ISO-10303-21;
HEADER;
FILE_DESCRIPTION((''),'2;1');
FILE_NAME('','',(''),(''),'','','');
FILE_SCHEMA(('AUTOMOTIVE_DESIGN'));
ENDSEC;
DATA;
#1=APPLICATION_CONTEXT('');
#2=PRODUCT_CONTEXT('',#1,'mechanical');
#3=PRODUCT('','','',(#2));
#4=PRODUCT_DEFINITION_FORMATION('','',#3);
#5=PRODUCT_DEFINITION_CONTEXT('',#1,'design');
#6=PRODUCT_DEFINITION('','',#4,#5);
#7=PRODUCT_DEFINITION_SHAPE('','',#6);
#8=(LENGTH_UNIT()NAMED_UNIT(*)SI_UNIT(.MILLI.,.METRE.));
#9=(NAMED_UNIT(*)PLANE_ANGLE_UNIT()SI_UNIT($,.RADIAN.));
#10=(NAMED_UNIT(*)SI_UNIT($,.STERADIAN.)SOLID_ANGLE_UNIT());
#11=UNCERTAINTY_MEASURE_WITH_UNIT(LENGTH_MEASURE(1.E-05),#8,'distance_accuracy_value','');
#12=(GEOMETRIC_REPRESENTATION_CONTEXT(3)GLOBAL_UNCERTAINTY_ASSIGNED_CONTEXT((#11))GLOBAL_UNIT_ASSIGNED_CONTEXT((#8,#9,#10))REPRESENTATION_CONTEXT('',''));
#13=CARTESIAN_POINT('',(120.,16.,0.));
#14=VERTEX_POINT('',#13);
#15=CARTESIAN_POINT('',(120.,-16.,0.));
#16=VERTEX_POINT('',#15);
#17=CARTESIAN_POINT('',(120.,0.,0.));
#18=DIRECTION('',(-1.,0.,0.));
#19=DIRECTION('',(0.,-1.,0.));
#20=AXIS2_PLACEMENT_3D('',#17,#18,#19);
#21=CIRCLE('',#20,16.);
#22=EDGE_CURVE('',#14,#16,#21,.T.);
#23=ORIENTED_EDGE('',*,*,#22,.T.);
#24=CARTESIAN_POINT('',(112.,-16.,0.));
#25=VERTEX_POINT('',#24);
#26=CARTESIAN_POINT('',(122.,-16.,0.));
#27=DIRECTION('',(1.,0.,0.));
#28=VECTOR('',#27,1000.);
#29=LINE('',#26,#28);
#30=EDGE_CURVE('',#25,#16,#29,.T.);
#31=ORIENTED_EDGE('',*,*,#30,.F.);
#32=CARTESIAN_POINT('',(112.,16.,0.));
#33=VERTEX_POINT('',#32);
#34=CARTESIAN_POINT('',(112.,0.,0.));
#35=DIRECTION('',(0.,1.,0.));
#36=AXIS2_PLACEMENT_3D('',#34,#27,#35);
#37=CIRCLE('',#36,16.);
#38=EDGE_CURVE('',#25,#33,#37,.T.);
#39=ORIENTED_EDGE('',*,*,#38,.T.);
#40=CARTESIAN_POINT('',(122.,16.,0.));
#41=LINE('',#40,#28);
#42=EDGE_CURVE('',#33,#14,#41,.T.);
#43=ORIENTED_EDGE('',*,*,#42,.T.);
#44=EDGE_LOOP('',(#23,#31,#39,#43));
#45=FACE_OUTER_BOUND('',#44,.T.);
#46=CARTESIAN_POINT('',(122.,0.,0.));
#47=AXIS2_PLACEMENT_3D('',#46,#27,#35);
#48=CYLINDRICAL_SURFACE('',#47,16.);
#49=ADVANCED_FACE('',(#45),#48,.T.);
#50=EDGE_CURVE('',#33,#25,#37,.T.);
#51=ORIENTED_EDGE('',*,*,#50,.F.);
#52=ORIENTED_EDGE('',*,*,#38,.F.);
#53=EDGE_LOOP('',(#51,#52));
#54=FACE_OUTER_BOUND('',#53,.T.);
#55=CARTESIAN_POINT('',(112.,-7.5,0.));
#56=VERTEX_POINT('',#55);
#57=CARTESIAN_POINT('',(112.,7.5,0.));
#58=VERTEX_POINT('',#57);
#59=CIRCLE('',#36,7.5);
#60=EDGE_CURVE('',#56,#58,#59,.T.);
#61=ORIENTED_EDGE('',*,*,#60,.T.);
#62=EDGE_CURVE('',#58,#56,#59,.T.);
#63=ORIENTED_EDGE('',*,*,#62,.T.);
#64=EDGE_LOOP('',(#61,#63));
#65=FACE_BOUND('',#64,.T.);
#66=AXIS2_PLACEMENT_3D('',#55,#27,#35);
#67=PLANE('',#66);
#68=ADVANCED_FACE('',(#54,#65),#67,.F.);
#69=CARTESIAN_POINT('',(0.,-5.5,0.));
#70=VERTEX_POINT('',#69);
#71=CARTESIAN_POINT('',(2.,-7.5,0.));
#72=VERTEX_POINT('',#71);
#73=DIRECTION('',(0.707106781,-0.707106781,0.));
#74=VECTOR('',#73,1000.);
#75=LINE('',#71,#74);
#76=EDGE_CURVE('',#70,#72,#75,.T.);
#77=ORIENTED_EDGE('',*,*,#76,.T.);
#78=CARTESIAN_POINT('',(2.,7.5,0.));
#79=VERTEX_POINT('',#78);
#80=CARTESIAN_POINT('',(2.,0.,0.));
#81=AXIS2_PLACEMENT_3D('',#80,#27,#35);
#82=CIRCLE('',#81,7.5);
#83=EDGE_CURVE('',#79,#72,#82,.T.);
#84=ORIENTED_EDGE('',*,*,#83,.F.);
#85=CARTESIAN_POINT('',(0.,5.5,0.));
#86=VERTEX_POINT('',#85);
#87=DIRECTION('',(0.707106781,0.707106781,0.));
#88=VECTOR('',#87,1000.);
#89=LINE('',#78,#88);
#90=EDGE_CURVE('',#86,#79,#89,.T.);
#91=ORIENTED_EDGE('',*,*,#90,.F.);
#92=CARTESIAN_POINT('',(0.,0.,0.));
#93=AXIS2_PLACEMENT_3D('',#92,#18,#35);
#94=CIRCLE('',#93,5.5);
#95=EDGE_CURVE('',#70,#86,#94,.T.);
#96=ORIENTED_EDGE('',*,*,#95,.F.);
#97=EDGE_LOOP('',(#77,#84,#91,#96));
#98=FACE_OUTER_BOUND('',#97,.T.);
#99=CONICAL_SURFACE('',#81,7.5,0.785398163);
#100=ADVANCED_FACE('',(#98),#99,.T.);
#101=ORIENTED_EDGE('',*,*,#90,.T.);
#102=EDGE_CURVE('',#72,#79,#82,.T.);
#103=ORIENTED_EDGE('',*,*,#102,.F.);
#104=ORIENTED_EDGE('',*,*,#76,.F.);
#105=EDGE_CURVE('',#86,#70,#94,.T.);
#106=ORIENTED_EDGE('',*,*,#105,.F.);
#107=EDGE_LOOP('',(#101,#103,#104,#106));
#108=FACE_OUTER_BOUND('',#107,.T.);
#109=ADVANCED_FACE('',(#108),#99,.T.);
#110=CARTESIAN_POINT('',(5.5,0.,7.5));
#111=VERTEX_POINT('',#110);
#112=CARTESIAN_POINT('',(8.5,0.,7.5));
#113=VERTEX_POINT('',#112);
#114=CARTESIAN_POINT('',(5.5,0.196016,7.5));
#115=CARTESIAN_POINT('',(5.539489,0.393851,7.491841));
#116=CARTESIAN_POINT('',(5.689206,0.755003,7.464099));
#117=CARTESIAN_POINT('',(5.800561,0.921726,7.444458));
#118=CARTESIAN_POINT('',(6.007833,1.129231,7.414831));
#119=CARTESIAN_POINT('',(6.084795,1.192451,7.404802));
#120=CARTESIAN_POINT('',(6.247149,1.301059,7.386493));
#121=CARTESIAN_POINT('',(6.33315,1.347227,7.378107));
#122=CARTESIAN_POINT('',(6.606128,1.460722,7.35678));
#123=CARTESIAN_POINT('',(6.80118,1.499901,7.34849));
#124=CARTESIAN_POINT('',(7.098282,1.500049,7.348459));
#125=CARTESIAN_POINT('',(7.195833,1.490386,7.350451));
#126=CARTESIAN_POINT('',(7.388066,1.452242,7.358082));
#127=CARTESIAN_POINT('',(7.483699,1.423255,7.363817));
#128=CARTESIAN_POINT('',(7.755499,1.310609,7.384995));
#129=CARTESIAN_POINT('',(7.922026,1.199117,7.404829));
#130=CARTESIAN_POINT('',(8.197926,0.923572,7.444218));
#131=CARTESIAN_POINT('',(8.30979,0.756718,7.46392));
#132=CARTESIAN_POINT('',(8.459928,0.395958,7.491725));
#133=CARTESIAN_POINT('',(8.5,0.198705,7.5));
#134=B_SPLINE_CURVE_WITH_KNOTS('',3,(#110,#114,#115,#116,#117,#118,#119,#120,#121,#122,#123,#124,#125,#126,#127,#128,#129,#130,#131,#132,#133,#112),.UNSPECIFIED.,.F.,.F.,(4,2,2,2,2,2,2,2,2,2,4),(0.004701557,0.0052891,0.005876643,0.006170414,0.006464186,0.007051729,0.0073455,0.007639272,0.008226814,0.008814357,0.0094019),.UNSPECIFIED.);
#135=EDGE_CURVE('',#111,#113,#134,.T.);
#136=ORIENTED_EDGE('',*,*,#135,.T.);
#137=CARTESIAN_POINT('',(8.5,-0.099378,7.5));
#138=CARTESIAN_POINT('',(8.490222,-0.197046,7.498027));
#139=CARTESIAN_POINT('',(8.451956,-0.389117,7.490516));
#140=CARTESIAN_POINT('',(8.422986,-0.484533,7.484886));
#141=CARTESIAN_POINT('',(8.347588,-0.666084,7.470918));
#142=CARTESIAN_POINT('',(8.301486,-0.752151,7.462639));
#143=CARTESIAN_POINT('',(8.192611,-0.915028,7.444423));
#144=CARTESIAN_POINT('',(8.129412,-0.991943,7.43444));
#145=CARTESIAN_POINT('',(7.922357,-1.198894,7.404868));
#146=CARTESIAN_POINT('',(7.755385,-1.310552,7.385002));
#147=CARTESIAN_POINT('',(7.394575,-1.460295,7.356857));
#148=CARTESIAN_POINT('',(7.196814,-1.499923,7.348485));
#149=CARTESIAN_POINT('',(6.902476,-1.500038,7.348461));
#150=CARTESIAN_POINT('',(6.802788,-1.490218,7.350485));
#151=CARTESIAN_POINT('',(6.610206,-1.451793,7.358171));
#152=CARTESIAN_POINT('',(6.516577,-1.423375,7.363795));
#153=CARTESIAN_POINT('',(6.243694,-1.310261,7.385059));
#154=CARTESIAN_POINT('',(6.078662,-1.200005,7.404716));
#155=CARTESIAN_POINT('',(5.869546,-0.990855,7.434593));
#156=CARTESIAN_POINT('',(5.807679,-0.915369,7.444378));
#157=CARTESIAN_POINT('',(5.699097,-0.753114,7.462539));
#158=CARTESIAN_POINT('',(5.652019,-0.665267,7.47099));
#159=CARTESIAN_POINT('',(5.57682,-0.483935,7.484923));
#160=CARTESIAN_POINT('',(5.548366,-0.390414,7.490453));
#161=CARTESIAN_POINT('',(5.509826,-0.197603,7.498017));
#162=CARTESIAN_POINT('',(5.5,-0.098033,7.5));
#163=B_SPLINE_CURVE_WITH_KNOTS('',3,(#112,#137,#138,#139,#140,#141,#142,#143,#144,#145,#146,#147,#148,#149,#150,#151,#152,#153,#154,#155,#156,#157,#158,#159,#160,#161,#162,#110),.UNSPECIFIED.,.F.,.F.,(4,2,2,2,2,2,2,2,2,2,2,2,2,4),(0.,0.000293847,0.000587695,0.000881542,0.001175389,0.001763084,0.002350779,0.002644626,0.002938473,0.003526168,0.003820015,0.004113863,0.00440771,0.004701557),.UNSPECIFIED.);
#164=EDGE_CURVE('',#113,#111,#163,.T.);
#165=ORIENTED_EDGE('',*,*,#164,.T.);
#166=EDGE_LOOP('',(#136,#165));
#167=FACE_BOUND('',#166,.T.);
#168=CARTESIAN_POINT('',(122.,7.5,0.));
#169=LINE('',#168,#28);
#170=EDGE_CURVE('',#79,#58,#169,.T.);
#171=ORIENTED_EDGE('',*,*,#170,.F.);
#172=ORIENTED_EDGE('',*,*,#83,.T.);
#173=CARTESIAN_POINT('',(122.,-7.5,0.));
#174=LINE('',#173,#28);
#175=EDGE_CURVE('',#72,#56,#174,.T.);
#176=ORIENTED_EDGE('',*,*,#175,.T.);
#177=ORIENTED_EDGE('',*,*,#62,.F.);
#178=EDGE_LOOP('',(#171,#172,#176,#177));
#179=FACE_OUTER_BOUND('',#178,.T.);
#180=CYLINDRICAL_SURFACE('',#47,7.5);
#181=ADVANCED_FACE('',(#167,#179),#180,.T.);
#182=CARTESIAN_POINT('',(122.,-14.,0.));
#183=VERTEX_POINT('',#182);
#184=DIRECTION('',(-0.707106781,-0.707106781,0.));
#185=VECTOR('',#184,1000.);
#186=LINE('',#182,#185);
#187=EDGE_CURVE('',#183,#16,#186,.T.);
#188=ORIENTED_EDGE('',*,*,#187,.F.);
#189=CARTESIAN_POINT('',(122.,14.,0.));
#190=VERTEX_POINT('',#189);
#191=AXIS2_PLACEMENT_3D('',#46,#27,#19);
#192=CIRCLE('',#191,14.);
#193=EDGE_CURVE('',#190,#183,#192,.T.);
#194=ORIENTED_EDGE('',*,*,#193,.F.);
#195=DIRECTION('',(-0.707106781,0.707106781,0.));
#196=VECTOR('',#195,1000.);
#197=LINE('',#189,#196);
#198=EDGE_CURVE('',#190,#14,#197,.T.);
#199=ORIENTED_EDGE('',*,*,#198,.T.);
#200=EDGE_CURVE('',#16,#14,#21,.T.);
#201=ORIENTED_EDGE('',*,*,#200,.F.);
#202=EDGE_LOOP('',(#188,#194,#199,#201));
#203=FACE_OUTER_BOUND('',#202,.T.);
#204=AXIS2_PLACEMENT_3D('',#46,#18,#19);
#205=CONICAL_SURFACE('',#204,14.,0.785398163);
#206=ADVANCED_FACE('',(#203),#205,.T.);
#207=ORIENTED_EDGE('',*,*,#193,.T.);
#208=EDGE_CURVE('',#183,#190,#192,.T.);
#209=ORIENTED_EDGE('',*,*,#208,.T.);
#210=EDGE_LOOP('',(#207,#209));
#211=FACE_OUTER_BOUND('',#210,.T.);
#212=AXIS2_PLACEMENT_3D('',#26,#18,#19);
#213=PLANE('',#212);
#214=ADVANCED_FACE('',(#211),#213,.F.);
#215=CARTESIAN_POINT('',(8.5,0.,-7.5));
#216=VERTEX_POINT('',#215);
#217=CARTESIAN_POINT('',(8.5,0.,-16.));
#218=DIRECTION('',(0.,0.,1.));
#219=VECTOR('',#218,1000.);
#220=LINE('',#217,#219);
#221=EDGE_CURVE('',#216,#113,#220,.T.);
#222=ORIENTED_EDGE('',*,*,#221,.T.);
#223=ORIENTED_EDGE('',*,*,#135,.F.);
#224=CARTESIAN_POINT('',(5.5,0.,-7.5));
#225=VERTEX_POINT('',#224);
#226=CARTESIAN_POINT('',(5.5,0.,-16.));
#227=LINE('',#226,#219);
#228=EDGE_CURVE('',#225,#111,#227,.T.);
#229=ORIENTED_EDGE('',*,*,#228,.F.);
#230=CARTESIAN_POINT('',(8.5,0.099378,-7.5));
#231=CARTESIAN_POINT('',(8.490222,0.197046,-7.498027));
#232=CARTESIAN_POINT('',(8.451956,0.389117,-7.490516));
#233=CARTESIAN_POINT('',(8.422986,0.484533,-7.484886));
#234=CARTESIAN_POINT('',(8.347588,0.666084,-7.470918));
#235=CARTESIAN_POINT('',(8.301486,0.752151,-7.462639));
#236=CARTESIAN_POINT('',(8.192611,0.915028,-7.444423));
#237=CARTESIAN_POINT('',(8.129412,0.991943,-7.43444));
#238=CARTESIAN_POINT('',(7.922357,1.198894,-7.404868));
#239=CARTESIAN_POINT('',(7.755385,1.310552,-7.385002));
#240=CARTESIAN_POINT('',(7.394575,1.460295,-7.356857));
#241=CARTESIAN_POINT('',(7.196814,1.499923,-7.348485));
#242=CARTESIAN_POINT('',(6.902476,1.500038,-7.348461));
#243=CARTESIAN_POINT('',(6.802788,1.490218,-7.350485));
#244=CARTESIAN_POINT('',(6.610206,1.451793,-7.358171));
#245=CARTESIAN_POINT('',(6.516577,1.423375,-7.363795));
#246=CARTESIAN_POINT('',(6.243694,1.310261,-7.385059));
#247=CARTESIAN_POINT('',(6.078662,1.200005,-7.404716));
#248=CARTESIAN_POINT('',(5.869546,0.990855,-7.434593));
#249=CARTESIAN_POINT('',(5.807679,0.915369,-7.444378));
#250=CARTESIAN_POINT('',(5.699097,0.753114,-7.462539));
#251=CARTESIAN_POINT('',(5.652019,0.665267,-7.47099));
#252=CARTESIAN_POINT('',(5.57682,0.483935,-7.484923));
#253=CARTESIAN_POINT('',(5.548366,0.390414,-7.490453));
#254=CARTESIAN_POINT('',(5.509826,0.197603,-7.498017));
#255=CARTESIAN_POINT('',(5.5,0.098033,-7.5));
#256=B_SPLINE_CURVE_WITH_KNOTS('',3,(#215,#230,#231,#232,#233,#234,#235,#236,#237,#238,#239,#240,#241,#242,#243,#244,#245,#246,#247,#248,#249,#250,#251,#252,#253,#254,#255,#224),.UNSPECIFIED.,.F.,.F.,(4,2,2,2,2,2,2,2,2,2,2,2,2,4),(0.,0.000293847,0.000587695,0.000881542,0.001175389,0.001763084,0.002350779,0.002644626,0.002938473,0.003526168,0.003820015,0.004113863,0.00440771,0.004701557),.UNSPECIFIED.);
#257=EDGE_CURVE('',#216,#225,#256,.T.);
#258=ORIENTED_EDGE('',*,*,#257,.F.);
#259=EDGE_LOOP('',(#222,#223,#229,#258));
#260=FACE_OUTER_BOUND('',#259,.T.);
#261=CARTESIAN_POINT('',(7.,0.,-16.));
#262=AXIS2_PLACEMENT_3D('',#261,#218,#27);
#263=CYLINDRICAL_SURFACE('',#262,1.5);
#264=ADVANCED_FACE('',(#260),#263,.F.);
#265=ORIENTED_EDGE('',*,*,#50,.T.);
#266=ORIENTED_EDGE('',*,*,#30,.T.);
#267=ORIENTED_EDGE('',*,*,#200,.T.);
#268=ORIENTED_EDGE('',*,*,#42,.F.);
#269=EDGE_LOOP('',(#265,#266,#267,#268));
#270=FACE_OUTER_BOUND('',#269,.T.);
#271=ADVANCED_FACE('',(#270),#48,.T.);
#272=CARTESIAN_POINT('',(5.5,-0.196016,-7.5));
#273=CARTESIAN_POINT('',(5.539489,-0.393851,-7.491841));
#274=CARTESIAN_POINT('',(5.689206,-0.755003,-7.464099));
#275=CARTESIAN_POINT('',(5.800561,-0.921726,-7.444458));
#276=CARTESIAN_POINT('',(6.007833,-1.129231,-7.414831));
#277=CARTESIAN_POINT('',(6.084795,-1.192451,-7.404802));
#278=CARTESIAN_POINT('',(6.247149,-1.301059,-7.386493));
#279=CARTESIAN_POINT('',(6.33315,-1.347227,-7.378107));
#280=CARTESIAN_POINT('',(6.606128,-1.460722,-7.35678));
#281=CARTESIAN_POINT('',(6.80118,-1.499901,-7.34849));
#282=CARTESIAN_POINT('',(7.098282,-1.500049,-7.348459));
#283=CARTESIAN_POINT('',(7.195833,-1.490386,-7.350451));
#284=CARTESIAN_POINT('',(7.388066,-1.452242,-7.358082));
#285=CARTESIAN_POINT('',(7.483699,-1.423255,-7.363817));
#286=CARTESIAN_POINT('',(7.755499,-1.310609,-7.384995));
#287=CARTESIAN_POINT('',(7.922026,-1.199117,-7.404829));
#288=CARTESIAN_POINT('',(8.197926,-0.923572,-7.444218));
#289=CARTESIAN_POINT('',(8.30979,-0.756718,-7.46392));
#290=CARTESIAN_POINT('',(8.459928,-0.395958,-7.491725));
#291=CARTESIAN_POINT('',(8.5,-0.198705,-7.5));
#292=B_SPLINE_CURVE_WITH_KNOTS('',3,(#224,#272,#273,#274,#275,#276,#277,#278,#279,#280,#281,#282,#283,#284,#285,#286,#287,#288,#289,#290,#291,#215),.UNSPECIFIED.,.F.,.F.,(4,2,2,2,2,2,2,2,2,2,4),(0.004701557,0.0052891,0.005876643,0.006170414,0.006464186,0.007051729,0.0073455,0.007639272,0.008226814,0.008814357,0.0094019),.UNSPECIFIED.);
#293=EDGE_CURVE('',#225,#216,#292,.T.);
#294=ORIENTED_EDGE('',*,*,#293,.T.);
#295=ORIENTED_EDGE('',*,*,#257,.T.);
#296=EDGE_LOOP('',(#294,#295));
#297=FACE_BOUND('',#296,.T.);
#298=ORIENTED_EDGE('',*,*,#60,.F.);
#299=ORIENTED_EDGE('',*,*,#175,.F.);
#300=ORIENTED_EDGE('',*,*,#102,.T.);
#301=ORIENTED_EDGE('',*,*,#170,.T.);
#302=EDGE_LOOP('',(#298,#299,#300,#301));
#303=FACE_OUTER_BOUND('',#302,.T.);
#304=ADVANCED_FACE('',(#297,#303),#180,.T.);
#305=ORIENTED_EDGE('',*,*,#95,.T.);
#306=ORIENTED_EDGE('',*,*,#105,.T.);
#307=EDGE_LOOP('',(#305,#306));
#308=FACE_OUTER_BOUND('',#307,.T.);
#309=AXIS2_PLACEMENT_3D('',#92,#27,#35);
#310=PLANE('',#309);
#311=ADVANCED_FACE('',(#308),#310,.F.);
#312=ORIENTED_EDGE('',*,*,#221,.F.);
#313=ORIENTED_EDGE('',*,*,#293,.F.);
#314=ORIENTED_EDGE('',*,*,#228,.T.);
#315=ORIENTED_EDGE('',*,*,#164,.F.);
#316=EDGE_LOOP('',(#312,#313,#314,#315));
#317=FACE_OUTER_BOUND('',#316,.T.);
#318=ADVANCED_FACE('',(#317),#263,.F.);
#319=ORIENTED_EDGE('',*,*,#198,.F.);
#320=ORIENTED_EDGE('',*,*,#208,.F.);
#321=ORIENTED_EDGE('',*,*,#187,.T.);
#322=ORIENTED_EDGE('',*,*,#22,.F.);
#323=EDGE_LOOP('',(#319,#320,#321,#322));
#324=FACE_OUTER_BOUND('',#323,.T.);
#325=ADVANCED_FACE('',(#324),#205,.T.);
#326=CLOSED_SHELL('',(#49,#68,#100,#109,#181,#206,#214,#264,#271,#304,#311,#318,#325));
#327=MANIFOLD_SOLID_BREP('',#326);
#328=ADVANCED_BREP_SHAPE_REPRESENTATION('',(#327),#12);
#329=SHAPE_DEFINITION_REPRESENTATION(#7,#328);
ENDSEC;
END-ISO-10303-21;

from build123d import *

# Parameters (mm, degrees)
CROSS_HOLE_3_DEPTH      = 125.080618954
CROSS_HOLE_3_DEPTH_BACK = 125.080618954
CROSS_HOLE_SKETCH_R     = 1.5
CHAMFER_2X45_SIZE       = 2


with BuildPart() as part:
    # Pin Profile Sketch → Pin Body (revolve)
    with BuildSketch(Plane.XY, mode=Mode.PRIVATE) as pin_body_sk:
        Polygon((0, -7.5), (112, -7.5), (112, -16), (122, -16), (122, 0), (0, 0), align=None)
    revolve(pin_body_sk.sketch.rotate(Axis((122, 0, 0), (-1, 0, 0)), 180), axis=Axis((122, 0, 0), (-1, 0, 0)))

    # Cross Hole Sketch → Cross Hole Ø3 (cut, two sides: drawn at the far end of the back side and taken through both)
    with BuildSketch(Plane.XY.offset(-CROSS_HOLE_3_DEPTH_BACK)):
        with Locations((7, 0)):
            Circle(CROSS_HOLE_SKETCH_R)
    extrude(amount=CROSS_HOLE_3_DEPTH + CROSS_HOLE_3_DEPTH_BACK, mode=Mode.SUBTRACT)

    # Chamfer 2x45°
    chamfer_2x45_edges = [part.edges().sort_by_distance(p)[0] for p in [
        (122, -16, 0),
        (0, -7.5, 0),
    ]]
    chamfer(chamfer_2x45_edges, length=CHAMFER_2X45_SIZE)


solid = part.part
